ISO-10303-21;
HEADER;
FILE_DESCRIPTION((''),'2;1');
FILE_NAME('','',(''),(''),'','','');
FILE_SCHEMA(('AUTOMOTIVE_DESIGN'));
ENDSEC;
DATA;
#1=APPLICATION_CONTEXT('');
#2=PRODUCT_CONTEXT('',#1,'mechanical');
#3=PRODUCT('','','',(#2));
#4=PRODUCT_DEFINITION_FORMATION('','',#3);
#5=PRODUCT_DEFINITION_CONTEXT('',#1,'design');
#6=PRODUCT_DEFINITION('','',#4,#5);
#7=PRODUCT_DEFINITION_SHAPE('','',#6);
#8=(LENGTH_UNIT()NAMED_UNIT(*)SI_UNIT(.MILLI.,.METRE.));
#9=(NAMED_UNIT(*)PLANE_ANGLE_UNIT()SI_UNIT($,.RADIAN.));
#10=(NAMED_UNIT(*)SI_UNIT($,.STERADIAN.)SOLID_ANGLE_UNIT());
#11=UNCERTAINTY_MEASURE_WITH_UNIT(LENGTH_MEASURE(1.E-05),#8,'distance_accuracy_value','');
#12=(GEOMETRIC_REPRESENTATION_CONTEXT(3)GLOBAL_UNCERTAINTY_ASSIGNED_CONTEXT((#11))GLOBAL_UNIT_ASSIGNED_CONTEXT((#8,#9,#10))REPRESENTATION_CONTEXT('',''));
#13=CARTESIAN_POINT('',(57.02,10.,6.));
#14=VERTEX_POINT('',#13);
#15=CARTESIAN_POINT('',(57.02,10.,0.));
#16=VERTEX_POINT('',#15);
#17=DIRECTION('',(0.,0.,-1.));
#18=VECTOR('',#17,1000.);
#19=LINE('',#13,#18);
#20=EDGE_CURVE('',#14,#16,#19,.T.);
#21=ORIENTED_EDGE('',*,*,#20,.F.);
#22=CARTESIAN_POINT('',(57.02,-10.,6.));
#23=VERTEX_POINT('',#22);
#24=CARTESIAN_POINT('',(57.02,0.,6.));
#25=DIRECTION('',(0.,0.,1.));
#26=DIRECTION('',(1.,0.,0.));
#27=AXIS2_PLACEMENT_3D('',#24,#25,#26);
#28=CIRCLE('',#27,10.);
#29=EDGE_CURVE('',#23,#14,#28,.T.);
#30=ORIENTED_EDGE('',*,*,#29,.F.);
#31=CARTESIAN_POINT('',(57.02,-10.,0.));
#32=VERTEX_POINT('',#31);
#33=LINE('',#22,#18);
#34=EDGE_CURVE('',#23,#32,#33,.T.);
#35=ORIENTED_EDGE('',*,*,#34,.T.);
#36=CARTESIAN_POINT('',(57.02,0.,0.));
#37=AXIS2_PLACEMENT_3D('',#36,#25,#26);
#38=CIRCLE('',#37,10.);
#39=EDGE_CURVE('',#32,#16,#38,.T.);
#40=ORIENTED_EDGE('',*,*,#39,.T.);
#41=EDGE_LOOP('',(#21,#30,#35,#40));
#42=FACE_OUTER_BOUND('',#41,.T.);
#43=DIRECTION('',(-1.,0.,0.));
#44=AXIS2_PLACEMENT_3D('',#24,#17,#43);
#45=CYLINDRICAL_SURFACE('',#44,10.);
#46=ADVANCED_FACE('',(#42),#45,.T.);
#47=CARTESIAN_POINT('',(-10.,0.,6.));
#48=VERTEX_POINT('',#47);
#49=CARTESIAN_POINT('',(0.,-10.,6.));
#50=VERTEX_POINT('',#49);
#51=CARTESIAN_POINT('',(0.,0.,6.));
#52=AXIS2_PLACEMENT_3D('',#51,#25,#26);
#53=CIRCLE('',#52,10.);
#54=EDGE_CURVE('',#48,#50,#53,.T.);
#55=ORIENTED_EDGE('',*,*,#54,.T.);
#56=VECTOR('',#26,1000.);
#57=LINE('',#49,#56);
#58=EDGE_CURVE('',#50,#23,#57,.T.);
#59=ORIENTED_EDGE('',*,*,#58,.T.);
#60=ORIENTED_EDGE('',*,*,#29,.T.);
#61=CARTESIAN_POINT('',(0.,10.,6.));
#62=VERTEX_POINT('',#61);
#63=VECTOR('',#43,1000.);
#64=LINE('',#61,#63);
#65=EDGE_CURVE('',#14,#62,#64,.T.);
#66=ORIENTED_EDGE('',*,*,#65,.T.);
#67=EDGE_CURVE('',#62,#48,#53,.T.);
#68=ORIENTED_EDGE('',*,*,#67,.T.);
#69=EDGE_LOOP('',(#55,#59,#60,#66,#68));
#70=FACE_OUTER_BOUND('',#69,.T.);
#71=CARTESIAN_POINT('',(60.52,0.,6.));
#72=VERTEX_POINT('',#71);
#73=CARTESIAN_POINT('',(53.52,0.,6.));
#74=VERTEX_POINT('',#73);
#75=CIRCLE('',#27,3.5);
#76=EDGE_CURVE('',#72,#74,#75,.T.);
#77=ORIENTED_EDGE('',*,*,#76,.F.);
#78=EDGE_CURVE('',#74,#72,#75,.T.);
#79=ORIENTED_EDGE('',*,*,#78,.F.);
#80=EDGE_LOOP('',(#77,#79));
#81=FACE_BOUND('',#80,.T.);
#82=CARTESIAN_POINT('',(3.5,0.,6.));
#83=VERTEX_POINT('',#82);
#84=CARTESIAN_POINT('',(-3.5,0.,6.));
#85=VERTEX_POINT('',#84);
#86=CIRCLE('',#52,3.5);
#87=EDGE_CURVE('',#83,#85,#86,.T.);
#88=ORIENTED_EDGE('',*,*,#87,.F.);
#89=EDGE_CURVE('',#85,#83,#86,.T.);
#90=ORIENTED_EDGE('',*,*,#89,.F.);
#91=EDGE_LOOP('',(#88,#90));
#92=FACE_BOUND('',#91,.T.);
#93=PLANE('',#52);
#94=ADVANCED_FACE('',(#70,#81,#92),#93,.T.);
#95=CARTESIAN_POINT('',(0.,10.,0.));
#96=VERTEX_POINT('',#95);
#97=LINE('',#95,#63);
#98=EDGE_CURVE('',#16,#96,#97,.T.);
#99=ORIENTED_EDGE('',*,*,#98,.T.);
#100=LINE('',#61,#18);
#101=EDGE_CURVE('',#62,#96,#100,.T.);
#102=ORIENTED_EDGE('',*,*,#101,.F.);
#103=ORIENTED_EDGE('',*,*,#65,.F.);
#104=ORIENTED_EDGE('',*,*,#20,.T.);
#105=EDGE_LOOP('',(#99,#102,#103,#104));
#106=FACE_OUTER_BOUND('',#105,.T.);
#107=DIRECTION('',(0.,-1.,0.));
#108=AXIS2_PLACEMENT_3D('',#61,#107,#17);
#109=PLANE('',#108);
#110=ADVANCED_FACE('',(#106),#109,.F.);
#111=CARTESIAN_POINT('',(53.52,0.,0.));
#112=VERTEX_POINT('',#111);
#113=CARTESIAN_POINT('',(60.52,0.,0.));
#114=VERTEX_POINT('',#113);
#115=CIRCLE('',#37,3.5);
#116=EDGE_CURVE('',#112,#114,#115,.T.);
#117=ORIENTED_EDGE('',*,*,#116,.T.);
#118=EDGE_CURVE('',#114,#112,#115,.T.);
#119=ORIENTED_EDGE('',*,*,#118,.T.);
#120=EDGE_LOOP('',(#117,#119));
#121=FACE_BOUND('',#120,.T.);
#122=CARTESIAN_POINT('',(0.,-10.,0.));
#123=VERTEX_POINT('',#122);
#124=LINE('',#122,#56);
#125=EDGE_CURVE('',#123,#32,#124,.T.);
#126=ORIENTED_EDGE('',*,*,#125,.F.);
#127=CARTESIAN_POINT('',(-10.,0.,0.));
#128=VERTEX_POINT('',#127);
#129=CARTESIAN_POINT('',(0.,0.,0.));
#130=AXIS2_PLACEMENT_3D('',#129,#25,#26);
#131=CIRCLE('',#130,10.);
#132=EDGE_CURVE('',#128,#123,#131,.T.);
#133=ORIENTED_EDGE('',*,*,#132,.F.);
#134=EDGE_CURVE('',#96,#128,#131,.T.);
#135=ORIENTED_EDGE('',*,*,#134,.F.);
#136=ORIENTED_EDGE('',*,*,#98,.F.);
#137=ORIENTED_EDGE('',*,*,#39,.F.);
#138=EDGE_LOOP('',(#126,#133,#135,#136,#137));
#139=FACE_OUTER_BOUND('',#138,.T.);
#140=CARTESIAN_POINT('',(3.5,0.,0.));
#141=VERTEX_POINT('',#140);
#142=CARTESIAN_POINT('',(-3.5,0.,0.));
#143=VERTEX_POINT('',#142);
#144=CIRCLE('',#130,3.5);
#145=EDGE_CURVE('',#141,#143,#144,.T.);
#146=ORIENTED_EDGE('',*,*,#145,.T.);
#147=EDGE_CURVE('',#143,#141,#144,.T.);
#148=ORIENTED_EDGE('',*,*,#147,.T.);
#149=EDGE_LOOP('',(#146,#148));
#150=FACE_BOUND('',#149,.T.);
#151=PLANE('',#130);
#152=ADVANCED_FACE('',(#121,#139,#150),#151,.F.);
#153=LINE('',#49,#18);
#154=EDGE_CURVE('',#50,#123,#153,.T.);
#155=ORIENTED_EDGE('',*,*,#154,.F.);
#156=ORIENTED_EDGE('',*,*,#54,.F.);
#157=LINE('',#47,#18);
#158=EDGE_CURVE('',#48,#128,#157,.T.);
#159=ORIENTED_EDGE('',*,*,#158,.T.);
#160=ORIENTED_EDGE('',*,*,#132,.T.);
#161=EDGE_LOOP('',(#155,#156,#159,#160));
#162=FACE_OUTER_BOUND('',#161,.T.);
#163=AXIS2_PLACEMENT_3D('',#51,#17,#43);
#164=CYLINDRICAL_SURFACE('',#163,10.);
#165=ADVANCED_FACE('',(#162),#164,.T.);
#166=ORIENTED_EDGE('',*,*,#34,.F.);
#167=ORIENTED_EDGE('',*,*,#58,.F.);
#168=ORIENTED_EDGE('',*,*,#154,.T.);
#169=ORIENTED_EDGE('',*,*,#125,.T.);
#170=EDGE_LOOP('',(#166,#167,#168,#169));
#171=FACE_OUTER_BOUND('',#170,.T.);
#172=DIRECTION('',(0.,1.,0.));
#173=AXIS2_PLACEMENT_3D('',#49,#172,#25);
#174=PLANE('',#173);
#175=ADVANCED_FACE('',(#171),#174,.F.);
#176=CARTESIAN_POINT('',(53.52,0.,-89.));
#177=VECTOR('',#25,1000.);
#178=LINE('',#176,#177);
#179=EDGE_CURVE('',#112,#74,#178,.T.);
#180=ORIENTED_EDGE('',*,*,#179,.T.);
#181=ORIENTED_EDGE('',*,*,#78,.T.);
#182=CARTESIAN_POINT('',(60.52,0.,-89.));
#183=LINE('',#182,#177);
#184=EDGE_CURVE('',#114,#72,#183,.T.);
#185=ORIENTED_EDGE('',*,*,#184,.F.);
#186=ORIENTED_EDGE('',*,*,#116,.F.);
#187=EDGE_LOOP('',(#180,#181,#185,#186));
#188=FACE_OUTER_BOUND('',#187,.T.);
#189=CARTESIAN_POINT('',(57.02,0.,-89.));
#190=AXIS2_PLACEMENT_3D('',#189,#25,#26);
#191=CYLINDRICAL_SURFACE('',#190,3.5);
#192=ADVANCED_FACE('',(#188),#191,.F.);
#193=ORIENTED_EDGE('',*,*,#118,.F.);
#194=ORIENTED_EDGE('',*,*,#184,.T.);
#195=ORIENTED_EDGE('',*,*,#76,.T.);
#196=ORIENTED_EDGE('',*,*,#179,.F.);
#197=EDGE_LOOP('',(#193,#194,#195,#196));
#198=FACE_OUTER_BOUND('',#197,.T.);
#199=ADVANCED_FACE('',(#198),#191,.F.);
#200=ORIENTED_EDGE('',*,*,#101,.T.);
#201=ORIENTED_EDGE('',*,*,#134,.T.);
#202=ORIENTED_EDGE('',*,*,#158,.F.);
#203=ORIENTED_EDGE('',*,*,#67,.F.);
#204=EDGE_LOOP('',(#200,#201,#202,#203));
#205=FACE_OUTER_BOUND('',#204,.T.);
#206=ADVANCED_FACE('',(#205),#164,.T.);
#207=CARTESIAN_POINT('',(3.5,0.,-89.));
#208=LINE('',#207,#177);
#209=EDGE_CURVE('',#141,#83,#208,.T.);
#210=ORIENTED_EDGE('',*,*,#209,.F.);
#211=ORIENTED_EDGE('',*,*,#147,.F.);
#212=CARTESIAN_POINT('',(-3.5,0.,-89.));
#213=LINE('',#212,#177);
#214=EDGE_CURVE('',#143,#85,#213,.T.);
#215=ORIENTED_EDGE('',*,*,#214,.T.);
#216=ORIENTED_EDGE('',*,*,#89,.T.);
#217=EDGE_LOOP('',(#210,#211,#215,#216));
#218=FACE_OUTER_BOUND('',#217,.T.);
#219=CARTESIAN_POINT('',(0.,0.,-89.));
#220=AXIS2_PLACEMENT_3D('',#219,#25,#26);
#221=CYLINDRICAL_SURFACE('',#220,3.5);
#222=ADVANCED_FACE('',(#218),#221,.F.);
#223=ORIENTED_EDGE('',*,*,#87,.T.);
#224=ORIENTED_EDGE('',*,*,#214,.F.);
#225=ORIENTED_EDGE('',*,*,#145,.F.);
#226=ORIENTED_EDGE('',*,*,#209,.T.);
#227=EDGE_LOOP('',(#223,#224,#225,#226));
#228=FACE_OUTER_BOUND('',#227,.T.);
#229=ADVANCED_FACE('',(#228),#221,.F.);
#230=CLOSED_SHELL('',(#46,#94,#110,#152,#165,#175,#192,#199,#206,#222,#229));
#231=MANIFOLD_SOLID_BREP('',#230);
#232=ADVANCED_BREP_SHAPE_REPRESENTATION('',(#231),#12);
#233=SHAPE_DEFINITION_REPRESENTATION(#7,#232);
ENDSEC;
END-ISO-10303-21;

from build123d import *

# Parameters (mm, degrees)
BOSS_EXTRUDE1_DEPTH = 6
SKETCH2_R           = 3.5
CUT_EXTRUDE1_DEPTH  = 95


with BuildPart() as part:
    # Sketch1 → Boss-Extrude1 (new body)
    with BuildSketch(Plane.XY):
        with BuildLine():
            Line((0, 10), (57.02, 10))
            ThreePointArc((57.02, 10), (67.02, 0), (57.02, -10))
            Line((57.02, -10), (0, -10))
            ThreePointArc((0, -10), (-10, 0), (0, 10))
        make_face()
    extrude(amount=BOSS_EXTRUDE1_DEPTH)

    # Sketch2 → Cut-Extrude1 (cut)
    with BuildSketch(Plane.XY.offset(6)):
        Circle(SKETCH2_R)
        with Locations((57.02, 0)):
            Circle(SKETCH2_R)
    extrude(amount=-CUT_EXTRUDE1_DEPTH, mode=Mode.SUBTRACT)


solid = part.part
